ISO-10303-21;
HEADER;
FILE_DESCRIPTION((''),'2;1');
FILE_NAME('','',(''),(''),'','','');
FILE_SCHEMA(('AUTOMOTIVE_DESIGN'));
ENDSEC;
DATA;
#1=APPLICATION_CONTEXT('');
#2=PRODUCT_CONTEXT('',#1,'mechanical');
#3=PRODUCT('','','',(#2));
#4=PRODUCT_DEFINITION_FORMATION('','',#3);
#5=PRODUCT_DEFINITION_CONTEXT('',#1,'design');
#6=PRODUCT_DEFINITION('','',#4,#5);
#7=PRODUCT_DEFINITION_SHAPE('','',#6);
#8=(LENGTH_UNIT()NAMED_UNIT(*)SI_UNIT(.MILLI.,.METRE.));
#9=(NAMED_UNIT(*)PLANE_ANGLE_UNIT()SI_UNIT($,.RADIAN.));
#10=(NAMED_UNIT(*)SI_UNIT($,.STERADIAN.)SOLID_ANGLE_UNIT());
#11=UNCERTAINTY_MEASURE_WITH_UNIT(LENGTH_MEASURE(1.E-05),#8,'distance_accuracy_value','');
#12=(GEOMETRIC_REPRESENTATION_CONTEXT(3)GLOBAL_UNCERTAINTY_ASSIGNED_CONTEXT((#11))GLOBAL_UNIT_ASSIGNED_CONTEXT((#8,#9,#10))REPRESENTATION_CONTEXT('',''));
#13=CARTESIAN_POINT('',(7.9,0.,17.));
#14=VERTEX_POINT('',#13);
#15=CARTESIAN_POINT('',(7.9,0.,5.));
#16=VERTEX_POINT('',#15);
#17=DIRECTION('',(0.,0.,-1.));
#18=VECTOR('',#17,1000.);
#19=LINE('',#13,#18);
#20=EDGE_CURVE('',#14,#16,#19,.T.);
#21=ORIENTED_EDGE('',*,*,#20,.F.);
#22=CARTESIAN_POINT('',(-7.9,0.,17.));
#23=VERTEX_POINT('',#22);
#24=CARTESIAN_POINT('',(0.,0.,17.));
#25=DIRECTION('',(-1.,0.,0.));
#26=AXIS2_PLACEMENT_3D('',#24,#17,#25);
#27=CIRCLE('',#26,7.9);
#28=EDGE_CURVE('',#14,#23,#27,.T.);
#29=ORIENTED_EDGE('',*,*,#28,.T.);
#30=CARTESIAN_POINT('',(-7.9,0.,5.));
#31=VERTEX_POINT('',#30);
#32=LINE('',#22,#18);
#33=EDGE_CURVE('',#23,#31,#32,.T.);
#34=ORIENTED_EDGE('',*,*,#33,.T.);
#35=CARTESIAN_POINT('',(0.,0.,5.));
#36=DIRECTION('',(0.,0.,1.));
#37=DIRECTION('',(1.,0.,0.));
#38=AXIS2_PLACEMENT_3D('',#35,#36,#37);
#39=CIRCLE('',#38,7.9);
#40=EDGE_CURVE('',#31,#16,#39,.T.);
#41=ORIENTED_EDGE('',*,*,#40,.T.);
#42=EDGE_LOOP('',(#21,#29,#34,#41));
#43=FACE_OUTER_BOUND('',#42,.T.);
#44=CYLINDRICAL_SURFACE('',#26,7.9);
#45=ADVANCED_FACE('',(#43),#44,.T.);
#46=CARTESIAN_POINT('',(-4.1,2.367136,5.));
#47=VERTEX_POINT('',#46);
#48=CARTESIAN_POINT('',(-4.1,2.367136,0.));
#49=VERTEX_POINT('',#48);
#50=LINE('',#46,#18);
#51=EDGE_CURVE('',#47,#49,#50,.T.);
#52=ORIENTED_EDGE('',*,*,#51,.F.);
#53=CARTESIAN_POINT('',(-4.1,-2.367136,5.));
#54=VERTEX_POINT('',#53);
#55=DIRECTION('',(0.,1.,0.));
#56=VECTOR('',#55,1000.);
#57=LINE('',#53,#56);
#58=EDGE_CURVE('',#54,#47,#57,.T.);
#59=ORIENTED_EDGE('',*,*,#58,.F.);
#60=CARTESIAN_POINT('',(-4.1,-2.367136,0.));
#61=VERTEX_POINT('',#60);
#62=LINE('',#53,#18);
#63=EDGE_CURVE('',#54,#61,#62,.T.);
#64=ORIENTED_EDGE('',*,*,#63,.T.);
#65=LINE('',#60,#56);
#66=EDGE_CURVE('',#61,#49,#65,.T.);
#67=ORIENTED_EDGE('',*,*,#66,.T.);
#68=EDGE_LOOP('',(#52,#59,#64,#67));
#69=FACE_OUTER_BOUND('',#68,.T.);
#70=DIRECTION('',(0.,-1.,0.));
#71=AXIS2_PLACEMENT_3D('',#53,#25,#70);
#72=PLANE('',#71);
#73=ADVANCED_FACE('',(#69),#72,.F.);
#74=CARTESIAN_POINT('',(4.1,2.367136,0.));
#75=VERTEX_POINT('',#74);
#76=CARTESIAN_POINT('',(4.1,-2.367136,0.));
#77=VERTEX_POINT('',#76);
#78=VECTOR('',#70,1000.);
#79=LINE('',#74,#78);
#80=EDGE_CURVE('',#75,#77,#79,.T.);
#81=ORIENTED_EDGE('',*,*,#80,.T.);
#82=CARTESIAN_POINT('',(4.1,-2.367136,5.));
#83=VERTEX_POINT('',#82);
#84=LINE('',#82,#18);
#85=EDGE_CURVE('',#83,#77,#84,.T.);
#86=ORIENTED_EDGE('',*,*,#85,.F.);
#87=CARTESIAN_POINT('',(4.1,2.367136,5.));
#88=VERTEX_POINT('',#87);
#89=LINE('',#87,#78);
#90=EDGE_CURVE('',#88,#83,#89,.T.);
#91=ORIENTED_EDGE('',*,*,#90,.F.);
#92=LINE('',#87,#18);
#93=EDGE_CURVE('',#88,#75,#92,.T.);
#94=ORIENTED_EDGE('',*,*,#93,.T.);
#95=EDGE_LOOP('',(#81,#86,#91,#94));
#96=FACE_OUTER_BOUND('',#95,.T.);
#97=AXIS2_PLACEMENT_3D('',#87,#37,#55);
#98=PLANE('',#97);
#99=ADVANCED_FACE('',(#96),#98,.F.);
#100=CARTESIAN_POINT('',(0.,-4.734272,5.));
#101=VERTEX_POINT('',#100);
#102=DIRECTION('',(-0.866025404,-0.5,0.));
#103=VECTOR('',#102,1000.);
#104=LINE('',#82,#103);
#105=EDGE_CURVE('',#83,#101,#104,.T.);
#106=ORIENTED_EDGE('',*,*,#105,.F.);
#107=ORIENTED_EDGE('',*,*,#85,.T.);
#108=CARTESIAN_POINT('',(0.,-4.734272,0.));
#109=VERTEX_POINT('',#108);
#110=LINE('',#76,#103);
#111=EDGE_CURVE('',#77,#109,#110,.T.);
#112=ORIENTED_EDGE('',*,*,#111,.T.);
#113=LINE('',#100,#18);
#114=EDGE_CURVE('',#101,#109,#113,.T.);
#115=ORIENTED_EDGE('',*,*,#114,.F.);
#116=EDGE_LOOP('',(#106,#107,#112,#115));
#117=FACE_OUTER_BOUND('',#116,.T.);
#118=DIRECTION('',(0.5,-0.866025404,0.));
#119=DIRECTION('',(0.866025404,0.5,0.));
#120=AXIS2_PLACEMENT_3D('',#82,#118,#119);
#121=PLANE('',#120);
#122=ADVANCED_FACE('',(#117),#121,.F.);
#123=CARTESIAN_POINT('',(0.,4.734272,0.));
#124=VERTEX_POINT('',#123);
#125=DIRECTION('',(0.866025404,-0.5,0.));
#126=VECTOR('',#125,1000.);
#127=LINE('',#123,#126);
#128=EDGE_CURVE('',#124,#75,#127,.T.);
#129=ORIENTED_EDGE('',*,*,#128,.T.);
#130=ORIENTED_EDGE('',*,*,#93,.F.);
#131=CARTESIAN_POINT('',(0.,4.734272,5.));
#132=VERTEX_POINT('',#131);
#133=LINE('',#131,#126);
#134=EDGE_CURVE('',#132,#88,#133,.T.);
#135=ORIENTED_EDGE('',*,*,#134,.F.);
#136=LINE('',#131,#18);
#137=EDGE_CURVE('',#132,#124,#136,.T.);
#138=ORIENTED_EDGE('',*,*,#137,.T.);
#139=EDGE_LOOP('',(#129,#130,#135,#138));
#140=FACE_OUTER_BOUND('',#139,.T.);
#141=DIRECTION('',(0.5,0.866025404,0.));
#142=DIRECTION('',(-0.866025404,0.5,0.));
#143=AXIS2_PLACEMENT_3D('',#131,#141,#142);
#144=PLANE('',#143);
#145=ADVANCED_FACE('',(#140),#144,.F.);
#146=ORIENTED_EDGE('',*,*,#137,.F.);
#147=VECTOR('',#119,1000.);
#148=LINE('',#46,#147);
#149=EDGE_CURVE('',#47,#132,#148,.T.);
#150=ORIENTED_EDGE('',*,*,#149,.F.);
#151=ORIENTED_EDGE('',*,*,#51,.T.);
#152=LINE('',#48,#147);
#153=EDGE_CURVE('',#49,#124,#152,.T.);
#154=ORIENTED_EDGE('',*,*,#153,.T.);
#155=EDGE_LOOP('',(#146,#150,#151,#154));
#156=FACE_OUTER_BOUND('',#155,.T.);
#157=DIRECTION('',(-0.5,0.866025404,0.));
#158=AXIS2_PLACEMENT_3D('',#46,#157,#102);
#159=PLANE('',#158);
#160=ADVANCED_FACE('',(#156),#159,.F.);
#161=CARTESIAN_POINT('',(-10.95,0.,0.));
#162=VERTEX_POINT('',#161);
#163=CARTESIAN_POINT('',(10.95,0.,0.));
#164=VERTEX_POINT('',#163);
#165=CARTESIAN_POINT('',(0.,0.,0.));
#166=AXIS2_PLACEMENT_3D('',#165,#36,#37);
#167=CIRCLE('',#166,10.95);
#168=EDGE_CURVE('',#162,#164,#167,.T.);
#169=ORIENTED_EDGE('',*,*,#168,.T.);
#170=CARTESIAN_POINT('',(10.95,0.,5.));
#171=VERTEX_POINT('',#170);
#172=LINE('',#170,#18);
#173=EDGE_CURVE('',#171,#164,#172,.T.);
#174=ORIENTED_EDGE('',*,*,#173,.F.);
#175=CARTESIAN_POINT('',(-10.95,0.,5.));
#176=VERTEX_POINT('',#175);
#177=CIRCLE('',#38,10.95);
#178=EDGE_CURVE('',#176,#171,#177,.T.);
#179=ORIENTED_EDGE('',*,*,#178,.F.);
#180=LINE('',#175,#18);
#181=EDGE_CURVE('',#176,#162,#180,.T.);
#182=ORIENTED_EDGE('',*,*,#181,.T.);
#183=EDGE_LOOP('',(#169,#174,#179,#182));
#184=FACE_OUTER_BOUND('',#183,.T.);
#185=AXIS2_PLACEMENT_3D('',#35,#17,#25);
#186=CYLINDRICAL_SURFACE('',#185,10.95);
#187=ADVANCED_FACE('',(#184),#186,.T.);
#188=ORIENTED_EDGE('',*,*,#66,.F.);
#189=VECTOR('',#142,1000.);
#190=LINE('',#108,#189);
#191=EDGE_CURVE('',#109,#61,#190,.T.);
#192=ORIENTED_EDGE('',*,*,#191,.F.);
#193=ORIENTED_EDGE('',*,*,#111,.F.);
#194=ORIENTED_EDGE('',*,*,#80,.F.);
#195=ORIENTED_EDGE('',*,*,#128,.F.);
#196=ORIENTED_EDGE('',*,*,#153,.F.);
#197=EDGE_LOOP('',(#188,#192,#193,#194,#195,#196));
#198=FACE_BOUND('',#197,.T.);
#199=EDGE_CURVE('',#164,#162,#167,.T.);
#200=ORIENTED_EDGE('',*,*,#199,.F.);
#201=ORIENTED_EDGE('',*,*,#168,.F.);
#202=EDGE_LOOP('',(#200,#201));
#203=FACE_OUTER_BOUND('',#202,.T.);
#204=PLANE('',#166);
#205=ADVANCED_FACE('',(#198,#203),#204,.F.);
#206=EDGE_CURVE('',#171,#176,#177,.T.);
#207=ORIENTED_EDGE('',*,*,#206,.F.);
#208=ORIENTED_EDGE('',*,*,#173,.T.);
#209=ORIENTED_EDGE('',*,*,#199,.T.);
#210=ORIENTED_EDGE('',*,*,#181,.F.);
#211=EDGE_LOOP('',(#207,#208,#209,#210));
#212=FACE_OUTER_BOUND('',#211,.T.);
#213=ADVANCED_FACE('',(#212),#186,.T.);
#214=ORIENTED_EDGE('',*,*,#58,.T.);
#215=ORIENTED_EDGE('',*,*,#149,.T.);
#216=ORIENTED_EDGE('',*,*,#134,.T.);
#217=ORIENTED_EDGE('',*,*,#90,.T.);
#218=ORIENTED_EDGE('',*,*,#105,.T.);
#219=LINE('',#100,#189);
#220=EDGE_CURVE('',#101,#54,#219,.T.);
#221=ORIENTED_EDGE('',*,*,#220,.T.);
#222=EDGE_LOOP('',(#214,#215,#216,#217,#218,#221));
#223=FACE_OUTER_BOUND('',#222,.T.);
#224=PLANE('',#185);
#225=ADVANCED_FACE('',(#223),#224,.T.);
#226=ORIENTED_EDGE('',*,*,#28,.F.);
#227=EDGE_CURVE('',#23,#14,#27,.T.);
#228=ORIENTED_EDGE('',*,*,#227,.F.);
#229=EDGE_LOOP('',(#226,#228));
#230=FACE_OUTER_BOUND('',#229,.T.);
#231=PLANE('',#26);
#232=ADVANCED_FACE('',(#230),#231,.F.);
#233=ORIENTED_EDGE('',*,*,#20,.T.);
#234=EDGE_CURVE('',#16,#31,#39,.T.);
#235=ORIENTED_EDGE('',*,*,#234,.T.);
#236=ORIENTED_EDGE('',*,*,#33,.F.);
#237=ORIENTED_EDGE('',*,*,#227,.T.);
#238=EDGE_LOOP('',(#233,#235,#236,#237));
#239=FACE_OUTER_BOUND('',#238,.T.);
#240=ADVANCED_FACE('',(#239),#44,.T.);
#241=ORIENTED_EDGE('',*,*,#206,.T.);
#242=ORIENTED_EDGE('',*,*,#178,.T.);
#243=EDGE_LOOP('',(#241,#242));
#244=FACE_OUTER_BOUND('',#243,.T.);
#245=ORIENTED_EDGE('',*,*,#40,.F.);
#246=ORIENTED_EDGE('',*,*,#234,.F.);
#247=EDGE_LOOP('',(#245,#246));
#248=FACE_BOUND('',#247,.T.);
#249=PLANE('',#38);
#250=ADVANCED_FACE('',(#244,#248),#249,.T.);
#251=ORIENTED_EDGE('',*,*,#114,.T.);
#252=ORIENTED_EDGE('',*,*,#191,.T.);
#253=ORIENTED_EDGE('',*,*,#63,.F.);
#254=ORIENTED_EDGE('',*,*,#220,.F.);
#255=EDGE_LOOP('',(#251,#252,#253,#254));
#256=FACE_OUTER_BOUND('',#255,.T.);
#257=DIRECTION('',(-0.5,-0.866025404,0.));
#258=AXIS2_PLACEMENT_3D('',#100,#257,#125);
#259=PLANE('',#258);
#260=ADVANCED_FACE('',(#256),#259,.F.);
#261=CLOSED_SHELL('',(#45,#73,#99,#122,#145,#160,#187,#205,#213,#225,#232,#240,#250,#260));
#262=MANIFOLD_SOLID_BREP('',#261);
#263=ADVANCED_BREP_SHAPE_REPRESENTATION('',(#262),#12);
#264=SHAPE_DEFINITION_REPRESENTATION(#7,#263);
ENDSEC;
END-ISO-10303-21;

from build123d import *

# Parameters (mm, degrees)
SKETCH_1_R          = 10.95
EXTRUDE_1_DEPTH     = 5
SKETCH_2_R          = 7.9
EXTRUDE_2_DEPTH     = 17
CUT_EXTRUDE_1_DEPTH = 5


with BuildPart() as part:
    # 草图1 → 凸台-拉伸1 (new body)
    with BuildSketch(Plane.XY):
        Circle(SKETCH_1_R)
    extrude(amount=EXTRUDE_1_DEPTH)

    # 草图2 → 凸台-拉伸2 (add)
    with BuildSketch(Plane(origin=(0, 0, 0), x_dir=(-1, 0, 0), z_dir=(0, 0, -1))):
        Circle(SKETCH_2_R)
    extrude(amount=-EXTRUDE_2_DEPTH)

    # 草图3 → 切除-拉伸1 (cut)
    with BuildSketch(Plane(origin=(0, 0, 0), x_dir=(-1, 0, 0), z_dir=(0, 0, -1))):
        Polygon((0, 4.734272207), (-4.1, 2.367136104), (-4.1, -2.367136104), (0, -4.734272207), (4.1, -2.367136104), (4.1, 2.367136104), align=None)
    extrude(amount=-CUT_EXTRUDE_1_DEPTH, mode=Mode.SUBTRACT)


solid = part.part
